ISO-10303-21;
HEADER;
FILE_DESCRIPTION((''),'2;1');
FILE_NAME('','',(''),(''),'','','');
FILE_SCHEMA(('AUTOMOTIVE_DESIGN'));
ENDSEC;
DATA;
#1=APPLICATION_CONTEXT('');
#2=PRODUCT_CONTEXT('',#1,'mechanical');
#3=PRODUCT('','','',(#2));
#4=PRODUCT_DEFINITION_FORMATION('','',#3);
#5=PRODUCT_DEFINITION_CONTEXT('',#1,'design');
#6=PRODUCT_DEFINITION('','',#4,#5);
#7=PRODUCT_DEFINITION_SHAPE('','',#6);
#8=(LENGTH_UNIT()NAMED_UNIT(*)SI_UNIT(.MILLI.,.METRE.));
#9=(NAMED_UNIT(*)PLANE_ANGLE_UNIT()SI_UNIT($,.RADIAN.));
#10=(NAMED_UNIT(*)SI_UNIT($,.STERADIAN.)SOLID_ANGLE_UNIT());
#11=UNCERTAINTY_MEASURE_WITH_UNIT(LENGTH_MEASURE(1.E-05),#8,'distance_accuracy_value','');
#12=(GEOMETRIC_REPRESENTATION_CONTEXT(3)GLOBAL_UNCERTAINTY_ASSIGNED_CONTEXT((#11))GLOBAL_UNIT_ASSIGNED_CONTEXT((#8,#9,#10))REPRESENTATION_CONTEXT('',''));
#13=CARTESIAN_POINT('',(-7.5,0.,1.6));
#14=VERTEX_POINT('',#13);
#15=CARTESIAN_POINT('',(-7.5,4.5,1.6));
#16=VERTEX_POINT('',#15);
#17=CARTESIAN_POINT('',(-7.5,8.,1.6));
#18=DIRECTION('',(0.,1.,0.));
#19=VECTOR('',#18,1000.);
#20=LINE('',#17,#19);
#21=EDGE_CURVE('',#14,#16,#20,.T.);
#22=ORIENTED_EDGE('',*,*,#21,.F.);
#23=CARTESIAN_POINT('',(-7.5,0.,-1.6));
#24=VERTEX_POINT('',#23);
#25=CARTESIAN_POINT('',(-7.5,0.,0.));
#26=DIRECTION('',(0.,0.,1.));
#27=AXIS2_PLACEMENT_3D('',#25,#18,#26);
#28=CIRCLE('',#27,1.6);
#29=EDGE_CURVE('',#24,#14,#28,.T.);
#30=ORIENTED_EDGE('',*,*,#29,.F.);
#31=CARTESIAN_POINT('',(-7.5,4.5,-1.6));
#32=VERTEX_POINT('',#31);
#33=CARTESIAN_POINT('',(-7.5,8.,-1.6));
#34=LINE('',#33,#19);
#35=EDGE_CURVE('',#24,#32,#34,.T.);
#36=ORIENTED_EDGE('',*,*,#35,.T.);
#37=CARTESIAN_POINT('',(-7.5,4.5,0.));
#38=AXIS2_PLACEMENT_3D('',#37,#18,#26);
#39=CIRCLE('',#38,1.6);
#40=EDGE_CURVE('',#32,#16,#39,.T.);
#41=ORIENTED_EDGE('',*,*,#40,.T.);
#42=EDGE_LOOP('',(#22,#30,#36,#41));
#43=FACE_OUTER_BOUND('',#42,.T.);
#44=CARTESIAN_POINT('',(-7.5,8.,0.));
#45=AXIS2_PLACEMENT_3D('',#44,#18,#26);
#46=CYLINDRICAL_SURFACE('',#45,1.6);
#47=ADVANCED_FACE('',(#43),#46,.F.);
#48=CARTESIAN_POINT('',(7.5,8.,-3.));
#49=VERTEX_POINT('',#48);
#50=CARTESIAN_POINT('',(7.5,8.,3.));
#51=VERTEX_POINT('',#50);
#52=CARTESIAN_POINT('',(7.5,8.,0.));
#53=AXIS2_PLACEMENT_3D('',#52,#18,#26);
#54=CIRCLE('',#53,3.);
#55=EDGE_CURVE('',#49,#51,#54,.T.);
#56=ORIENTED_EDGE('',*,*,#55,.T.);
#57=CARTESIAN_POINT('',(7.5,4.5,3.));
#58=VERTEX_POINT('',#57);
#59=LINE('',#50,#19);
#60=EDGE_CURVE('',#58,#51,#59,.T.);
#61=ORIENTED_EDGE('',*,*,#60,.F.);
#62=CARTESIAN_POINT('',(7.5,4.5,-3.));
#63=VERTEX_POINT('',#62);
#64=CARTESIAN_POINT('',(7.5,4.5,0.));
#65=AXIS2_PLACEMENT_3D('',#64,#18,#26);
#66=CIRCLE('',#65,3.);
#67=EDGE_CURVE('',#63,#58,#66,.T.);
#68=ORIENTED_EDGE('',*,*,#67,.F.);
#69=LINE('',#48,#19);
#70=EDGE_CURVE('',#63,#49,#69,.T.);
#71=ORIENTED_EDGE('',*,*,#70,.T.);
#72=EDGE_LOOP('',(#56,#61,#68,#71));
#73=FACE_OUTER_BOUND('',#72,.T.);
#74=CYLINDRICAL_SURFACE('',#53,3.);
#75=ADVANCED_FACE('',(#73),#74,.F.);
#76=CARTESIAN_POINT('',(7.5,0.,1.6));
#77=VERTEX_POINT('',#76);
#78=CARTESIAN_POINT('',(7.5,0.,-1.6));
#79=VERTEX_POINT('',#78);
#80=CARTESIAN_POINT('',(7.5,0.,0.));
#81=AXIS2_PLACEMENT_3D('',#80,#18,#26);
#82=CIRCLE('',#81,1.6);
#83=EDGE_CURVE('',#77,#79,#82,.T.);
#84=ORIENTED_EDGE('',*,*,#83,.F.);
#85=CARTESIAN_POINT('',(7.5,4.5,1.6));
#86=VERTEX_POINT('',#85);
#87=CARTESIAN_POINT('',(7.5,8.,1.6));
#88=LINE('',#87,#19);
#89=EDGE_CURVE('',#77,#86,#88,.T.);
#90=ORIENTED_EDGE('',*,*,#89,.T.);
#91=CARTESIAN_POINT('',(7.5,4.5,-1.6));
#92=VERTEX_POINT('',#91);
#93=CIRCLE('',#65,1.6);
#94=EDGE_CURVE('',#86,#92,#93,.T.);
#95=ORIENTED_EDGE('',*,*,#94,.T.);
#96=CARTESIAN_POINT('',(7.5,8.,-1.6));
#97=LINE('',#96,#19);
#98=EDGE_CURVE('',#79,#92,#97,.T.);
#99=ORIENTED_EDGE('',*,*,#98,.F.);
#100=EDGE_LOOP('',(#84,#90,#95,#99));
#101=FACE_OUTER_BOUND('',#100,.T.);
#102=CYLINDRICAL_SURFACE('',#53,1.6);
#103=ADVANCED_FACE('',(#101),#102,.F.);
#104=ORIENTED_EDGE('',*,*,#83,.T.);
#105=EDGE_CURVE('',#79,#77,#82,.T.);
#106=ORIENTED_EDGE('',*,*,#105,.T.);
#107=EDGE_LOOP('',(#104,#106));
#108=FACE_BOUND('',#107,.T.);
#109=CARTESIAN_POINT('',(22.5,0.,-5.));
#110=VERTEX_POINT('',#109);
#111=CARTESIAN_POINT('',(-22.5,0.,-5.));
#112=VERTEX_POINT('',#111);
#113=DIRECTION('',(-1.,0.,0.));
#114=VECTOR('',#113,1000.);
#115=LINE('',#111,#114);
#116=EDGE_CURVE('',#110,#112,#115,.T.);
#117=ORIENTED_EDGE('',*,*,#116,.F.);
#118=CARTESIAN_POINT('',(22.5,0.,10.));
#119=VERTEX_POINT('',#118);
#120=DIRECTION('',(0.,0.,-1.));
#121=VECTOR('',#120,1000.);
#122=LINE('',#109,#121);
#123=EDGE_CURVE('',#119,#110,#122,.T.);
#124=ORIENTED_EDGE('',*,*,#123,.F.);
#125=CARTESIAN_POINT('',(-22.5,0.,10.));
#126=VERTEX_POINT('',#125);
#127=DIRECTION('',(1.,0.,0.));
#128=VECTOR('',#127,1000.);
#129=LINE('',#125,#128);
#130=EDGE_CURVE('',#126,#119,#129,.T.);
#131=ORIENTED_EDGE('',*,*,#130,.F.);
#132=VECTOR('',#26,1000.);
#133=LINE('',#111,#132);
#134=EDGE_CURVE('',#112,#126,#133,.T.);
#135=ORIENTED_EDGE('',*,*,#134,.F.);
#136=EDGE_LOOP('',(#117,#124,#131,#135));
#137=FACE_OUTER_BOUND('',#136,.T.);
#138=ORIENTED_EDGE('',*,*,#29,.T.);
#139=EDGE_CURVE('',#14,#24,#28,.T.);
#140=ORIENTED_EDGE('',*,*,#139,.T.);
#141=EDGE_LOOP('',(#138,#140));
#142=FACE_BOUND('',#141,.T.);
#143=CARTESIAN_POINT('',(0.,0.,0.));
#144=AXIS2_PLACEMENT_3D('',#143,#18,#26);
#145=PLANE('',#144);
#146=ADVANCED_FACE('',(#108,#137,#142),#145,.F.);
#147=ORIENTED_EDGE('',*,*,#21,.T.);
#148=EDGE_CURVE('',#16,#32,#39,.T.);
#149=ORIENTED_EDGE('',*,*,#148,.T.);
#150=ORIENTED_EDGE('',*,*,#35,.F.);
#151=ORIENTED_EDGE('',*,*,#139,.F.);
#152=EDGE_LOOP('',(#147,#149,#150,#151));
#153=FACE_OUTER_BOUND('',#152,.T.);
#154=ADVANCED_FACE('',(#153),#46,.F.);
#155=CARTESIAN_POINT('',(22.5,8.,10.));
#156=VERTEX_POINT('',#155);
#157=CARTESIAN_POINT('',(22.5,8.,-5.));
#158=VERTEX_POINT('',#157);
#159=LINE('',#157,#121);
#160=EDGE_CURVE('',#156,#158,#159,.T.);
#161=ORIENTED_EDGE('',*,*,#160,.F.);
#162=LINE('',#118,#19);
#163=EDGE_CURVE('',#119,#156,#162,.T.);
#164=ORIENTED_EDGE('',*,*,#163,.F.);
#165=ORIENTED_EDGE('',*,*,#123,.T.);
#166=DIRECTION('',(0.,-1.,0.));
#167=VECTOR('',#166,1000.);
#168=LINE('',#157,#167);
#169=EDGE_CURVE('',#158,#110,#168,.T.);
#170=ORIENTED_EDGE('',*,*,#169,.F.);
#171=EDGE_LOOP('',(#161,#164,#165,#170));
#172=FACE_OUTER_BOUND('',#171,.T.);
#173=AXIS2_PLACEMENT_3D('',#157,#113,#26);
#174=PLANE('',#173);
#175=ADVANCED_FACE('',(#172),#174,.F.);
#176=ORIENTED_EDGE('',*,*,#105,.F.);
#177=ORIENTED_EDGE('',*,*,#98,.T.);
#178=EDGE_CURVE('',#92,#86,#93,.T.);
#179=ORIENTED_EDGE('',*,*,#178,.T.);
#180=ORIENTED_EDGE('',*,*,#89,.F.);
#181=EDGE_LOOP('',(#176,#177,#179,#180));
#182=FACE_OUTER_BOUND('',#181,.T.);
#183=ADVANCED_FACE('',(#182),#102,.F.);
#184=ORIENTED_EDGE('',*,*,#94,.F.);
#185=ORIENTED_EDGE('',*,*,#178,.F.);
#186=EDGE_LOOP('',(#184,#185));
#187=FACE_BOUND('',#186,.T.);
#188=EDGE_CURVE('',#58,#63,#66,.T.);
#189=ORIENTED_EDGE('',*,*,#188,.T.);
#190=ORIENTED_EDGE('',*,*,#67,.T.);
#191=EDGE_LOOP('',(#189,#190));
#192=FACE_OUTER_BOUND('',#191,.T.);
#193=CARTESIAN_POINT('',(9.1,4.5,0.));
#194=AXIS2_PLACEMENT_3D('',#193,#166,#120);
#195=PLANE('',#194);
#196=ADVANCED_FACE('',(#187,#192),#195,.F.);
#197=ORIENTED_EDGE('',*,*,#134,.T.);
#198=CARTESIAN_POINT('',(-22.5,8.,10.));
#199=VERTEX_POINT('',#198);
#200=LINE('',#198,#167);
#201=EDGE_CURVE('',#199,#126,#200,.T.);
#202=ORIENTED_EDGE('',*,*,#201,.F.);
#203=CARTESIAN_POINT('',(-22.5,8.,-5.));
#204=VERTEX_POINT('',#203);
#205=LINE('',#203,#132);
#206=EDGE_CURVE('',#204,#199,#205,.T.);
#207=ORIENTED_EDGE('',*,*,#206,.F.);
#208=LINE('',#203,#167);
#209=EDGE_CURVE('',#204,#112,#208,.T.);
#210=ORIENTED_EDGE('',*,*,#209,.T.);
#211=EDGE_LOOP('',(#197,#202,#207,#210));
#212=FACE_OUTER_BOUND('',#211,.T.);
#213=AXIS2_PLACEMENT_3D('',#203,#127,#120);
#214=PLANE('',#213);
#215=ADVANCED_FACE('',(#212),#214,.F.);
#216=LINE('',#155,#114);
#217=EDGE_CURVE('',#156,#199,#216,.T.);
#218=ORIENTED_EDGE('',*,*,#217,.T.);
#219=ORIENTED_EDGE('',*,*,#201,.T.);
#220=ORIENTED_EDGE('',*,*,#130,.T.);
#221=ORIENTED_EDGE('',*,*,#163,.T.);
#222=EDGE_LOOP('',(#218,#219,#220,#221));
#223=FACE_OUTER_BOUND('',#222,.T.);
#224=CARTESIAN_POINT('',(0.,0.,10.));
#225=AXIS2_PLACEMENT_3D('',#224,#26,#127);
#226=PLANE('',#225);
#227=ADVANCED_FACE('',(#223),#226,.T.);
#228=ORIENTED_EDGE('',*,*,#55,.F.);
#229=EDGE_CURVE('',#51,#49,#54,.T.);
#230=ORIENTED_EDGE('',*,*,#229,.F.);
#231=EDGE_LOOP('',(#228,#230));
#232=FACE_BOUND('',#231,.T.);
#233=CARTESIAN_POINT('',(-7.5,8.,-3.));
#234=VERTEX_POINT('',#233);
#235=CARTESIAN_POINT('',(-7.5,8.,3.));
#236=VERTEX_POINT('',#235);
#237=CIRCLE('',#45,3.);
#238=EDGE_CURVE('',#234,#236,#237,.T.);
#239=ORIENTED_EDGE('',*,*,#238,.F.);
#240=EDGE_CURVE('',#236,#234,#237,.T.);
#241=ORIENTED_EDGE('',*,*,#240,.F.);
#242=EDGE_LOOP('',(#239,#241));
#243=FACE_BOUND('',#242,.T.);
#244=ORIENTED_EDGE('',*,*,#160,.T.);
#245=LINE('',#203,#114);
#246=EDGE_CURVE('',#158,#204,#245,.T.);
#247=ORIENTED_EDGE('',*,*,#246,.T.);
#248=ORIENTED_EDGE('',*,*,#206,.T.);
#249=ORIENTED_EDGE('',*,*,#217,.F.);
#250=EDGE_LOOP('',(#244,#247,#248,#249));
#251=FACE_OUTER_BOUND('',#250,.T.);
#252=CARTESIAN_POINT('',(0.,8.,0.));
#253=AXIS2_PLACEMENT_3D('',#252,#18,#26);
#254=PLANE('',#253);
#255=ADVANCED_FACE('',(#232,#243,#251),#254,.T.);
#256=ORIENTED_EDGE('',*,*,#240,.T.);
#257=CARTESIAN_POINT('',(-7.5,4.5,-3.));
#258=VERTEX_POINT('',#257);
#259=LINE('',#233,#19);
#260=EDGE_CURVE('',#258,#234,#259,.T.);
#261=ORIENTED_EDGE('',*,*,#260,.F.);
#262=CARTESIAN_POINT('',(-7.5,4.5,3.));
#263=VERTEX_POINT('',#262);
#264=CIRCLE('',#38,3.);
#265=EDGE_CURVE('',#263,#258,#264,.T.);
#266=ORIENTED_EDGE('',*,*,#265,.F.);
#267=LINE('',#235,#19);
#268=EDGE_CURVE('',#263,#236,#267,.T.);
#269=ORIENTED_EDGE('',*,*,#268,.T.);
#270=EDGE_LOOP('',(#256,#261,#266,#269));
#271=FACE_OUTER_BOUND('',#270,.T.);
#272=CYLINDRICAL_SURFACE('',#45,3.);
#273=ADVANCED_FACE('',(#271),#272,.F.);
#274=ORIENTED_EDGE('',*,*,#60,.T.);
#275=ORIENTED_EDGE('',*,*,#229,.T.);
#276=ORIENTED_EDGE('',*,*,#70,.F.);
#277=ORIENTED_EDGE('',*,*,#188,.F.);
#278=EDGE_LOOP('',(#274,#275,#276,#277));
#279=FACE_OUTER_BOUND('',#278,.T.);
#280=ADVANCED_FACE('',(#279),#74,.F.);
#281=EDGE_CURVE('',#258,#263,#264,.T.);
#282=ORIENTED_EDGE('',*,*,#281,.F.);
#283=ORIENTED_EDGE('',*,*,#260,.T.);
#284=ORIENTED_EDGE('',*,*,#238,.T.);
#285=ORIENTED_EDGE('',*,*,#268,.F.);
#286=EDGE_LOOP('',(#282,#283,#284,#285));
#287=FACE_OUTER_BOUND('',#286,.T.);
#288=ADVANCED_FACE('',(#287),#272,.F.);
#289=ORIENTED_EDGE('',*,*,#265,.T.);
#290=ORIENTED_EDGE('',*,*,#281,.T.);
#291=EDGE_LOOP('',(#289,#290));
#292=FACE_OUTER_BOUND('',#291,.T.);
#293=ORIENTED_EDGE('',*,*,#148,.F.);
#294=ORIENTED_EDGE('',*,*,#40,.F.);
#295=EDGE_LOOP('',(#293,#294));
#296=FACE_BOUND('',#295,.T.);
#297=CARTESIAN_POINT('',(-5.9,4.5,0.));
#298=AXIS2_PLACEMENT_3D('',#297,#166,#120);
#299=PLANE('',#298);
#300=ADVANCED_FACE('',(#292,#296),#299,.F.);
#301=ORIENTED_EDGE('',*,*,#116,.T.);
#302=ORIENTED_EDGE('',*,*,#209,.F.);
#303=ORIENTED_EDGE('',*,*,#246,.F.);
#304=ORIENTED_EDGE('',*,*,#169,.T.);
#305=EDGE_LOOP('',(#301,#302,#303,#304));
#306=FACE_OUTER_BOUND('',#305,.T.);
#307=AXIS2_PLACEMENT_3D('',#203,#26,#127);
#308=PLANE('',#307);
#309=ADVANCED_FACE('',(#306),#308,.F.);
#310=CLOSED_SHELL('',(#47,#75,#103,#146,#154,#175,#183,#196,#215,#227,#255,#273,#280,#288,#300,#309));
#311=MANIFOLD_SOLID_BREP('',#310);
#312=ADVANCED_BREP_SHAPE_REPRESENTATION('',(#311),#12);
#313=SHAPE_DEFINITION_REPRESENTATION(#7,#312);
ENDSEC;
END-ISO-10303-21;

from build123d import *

# Parameters (mm, degrees)
SKETCH_1_W                = 45
SKETCH_1_H                = 10
EXTRUDE_1_DEPTH           = 8
HOLE_WIZARD_1_D           = 3.2
HOLE_WIZARD_1_CBORE_D     = 6
HOLE_WIZARD_1_CBORE_DEPTH = 3.5
SKETCH_4_W                = 45
SKETCH_4_H                = 8
EXTRUDE_2_DEPTH           = 5


with BuildPart() as part:
    # 草图1 → 凸台-拉伸1 (new body)
    with BuildSketch(Plane(origin=(0, 0, 0), x_dir=(1, 0, 0), z_dir=(0, 1, 0))):
        Rectangle(SKETCH_1_W, SKETCH_1_H)
    extrude(amount=EXTRUDE_1_DEPTH)

    # 打孔尺寸(%根据)开槽圆柱头螺钉的类型1 (through all)
    with Locations(Plane(origin=(0, 8, 0), x_dir=(1, 0, 0), z_dir=(0, 1, 0))):
        with Locations((-7.5, 0), (7.5, 0)):
            CounterBoreHole(HOLE_WIZARD_1_D / 2, HOLE_WIZARD_1_CBORE_D / 2, HOLE_WIZARD_1_CBORE_DEPTH)

    # 草图4 → 凸台-拉伸2 (add)
    with BuildSketch(Plane.XY.offset(5)):
        with Locations((0, 4)):
            Rectangle(SKETCH_4_W, SKETCH_4_H)
    extrude(amount=EXTRUDE_2_DEPTH)


solid = part.part
